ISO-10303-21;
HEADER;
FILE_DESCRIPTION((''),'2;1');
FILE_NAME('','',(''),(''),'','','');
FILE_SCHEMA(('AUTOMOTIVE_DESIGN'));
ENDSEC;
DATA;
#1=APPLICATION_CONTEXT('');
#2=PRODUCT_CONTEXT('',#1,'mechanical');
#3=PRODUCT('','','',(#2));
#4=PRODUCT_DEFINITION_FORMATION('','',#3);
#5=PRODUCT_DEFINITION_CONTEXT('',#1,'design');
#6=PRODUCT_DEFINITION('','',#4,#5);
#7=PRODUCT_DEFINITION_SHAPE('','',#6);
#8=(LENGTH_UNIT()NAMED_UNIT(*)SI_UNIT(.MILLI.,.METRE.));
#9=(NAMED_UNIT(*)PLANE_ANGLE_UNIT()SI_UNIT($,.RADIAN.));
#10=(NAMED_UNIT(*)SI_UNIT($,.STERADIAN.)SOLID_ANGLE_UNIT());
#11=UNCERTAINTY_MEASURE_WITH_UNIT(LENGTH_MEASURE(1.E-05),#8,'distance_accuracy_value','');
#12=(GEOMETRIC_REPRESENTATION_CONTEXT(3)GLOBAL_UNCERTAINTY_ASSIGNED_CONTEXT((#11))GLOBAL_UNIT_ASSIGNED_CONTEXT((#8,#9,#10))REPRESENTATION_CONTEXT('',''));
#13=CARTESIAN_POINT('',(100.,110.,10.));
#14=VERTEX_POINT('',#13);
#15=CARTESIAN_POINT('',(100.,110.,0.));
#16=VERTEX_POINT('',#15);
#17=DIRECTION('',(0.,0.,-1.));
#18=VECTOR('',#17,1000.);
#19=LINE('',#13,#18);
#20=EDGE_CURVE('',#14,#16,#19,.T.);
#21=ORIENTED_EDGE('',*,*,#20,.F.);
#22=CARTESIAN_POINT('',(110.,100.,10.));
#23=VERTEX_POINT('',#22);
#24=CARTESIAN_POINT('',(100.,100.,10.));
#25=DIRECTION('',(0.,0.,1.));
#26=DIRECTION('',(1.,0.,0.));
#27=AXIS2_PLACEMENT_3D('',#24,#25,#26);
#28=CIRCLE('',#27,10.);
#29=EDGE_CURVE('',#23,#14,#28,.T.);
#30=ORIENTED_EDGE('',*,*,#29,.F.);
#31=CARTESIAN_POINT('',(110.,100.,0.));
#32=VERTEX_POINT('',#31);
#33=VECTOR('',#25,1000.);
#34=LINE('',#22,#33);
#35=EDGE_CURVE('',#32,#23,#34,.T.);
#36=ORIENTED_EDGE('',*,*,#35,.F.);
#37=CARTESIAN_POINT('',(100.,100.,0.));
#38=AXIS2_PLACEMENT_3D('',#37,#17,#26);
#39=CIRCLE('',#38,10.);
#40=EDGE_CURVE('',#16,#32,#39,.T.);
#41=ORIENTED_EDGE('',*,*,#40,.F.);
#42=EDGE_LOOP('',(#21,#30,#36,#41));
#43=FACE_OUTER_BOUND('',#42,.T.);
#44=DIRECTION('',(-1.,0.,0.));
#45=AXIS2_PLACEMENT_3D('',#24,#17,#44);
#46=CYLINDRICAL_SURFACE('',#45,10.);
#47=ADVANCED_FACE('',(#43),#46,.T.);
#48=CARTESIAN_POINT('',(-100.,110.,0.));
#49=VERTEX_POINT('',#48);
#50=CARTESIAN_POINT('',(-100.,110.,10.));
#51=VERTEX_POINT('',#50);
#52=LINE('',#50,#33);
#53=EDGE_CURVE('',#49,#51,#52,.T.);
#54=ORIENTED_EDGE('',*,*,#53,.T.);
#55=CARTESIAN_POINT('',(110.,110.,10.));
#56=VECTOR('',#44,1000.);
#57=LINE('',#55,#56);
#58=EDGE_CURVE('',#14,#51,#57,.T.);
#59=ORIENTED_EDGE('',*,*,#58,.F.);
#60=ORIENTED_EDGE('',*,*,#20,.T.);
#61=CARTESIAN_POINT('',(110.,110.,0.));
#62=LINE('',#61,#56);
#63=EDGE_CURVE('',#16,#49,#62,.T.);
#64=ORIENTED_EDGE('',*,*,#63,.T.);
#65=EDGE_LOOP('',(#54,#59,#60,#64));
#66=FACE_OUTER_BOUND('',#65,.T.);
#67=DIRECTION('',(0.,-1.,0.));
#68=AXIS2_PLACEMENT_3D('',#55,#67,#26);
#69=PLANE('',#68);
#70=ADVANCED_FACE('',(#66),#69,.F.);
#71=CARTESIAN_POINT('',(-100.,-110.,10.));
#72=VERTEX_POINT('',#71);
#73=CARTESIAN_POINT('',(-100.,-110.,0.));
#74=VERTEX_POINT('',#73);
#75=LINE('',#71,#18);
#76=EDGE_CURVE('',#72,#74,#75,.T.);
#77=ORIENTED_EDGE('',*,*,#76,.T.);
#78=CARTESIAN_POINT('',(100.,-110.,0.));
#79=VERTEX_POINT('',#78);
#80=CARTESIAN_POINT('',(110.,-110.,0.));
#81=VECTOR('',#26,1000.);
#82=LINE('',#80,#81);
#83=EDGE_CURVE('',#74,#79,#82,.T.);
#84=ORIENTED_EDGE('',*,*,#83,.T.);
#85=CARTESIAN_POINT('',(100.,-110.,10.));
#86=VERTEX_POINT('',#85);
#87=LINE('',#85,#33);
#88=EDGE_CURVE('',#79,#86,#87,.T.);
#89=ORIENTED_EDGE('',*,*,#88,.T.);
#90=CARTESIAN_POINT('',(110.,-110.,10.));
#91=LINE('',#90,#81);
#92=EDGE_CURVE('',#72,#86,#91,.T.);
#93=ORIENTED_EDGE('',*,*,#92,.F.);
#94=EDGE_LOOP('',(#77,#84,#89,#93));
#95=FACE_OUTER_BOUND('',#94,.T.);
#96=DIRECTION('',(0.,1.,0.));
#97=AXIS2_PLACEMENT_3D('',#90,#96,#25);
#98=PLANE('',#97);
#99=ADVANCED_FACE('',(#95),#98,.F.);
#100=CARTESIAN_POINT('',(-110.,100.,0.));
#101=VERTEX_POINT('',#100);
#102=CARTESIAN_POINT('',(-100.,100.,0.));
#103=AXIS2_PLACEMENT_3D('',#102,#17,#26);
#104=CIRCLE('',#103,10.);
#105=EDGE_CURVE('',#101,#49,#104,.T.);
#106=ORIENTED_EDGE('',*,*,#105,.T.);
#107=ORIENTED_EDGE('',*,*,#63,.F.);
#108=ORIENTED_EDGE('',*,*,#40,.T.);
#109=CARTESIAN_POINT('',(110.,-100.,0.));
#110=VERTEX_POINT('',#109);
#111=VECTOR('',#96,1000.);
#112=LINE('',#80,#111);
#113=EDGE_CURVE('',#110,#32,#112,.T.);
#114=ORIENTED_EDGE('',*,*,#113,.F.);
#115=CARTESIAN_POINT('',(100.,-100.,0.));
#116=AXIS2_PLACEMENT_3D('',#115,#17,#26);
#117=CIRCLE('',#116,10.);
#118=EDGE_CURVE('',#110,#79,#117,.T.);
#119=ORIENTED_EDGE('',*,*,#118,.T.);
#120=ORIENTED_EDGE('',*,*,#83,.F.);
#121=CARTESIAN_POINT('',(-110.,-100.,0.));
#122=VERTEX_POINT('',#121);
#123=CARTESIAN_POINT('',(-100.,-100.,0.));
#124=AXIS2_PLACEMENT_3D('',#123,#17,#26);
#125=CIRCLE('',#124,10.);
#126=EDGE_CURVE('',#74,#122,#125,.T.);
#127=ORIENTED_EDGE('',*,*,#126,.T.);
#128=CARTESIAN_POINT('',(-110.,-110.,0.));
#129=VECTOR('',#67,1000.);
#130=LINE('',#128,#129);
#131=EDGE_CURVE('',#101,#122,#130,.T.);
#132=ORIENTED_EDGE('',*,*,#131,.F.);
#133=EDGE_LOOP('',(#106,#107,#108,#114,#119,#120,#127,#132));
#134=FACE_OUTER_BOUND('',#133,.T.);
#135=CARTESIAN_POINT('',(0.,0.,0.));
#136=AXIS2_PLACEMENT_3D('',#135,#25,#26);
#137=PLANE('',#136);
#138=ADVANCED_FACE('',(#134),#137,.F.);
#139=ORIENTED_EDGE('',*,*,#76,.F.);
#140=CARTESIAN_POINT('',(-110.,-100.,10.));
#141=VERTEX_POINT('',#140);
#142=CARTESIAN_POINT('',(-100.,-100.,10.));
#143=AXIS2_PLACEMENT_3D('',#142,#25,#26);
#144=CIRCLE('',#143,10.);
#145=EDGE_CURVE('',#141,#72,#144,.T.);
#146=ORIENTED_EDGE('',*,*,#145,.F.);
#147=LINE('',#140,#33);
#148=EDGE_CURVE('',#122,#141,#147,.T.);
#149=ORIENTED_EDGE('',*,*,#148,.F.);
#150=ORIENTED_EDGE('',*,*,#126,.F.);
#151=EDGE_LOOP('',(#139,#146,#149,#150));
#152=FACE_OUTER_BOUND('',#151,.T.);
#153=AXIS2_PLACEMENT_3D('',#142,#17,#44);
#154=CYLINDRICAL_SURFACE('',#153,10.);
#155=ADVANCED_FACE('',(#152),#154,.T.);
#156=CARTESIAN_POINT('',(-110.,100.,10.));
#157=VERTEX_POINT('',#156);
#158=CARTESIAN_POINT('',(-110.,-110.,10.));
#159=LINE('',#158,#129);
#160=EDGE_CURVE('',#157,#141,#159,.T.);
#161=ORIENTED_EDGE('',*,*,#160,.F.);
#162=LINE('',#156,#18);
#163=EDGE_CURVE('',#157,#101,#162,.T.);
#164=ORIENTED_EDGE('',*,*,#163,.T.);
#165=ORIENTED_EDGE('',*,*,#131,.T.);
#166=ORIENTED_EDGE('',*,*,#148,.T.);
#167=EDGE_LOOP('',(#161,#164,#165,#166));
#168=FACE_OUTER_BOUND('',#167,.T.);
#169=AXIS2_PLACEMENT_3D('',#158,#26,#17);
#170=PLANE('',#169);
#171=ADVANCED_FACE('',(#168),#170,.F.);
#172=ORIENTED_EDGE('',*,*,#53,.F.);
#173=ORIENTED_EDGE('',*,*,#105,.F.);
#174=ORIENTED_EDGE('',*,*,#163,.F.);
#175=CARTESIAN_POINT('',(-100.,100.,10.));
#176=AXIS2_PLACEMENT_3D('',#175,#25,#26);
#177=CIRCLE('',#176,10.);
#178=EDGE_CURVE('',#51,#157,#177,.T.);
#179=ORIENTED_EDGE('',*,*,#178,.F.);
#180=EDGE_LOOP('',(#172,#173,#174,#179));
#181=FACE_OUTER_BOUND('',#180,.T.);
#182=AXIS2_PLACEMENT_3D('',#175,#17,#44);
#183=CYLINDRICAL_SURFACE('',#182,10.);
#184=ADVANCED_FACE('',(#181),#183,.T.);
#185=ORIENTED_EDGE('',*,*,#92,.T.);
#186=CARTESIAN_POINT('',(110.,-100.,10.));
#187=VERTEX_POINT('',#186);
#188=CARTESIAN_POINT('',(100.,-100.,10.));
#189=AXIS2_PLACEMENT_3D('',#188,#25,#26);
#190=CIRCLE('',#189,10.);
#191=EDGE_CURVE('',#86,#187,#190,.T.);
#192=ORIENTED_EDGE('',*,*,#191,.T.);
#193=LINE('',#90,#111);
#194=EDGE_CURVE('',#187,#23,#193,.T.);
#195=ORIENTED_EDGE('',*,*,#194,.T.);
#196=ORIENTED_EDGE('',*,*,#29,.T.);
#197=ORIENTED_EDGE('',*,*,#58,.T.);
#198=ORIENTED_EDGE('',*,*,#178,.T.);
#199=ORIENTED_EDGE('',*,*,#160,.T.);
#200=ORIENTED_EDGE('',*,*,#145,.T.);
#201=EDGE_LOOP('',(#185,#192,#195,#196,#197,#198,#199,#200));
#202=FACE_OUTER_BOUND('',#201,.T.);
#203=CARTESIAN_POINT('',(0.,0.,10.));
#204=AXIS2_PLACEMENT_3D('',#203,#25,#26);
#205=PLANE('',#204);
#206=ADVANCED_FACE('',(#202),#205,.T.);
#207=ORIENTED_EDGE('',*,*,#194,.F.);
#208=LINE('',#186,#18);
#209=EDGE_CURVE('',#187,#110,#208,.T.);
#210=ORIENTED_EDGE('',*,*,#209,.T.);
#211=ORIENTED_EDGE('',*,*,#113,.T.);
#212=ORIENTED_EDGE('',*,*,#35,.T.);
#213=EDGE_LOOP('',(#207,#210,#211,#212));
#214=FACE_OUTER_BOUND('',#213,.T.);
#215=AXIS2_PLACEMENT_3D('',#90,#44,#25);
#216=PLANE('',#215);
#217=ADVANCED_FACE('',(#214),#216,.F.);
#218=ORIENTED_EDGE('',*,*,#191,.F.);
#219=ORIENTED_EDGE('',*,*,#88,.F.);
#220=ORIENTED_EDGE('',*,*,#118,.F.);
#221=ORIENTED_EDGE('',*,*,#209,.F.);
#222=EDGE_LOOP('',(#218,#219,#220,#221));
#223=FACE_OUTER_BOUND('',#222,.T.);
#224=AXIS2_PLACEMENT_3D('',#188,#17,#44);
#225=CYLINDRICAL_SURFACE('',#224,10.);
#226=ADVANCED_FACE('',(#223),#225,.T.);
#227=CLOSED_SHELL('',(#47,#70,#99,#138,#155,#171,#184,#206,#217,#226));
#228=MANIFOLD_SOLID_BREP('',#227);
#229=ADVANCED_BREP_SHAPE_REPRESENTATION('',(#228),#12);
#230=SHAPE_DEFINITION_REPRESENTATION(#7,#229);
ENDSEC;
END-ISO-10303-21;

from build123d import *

# Parameters (mm, degrees)
SKETCH_1_W      = 220
SKETCH_1_H      = 220
EXTRUDE_1_DEPTH = 10
FILLET_1_R      = 10


with BuildPart() as part:
    # 草图1 → 凸台-拉伸1 (new body)
    with BuildSketch(Plane.XY):
        Rectangle(SKETCH_1_W, SKETCH_1_H)
    extrude(amount=EXTRUDE_1_DEPTH)

    # 圆角1
    fillet_1_edges = [part.edges().sort_by_distance(p)[0] for p in [
        (-110, 110, 5),
        (110, 110, 5),
        (110, -110, 5),
        (-110, -110, 5),
    ]]
    fillet(fillet_1_edges, radius=FILLET_1_R)


solid = part.part
